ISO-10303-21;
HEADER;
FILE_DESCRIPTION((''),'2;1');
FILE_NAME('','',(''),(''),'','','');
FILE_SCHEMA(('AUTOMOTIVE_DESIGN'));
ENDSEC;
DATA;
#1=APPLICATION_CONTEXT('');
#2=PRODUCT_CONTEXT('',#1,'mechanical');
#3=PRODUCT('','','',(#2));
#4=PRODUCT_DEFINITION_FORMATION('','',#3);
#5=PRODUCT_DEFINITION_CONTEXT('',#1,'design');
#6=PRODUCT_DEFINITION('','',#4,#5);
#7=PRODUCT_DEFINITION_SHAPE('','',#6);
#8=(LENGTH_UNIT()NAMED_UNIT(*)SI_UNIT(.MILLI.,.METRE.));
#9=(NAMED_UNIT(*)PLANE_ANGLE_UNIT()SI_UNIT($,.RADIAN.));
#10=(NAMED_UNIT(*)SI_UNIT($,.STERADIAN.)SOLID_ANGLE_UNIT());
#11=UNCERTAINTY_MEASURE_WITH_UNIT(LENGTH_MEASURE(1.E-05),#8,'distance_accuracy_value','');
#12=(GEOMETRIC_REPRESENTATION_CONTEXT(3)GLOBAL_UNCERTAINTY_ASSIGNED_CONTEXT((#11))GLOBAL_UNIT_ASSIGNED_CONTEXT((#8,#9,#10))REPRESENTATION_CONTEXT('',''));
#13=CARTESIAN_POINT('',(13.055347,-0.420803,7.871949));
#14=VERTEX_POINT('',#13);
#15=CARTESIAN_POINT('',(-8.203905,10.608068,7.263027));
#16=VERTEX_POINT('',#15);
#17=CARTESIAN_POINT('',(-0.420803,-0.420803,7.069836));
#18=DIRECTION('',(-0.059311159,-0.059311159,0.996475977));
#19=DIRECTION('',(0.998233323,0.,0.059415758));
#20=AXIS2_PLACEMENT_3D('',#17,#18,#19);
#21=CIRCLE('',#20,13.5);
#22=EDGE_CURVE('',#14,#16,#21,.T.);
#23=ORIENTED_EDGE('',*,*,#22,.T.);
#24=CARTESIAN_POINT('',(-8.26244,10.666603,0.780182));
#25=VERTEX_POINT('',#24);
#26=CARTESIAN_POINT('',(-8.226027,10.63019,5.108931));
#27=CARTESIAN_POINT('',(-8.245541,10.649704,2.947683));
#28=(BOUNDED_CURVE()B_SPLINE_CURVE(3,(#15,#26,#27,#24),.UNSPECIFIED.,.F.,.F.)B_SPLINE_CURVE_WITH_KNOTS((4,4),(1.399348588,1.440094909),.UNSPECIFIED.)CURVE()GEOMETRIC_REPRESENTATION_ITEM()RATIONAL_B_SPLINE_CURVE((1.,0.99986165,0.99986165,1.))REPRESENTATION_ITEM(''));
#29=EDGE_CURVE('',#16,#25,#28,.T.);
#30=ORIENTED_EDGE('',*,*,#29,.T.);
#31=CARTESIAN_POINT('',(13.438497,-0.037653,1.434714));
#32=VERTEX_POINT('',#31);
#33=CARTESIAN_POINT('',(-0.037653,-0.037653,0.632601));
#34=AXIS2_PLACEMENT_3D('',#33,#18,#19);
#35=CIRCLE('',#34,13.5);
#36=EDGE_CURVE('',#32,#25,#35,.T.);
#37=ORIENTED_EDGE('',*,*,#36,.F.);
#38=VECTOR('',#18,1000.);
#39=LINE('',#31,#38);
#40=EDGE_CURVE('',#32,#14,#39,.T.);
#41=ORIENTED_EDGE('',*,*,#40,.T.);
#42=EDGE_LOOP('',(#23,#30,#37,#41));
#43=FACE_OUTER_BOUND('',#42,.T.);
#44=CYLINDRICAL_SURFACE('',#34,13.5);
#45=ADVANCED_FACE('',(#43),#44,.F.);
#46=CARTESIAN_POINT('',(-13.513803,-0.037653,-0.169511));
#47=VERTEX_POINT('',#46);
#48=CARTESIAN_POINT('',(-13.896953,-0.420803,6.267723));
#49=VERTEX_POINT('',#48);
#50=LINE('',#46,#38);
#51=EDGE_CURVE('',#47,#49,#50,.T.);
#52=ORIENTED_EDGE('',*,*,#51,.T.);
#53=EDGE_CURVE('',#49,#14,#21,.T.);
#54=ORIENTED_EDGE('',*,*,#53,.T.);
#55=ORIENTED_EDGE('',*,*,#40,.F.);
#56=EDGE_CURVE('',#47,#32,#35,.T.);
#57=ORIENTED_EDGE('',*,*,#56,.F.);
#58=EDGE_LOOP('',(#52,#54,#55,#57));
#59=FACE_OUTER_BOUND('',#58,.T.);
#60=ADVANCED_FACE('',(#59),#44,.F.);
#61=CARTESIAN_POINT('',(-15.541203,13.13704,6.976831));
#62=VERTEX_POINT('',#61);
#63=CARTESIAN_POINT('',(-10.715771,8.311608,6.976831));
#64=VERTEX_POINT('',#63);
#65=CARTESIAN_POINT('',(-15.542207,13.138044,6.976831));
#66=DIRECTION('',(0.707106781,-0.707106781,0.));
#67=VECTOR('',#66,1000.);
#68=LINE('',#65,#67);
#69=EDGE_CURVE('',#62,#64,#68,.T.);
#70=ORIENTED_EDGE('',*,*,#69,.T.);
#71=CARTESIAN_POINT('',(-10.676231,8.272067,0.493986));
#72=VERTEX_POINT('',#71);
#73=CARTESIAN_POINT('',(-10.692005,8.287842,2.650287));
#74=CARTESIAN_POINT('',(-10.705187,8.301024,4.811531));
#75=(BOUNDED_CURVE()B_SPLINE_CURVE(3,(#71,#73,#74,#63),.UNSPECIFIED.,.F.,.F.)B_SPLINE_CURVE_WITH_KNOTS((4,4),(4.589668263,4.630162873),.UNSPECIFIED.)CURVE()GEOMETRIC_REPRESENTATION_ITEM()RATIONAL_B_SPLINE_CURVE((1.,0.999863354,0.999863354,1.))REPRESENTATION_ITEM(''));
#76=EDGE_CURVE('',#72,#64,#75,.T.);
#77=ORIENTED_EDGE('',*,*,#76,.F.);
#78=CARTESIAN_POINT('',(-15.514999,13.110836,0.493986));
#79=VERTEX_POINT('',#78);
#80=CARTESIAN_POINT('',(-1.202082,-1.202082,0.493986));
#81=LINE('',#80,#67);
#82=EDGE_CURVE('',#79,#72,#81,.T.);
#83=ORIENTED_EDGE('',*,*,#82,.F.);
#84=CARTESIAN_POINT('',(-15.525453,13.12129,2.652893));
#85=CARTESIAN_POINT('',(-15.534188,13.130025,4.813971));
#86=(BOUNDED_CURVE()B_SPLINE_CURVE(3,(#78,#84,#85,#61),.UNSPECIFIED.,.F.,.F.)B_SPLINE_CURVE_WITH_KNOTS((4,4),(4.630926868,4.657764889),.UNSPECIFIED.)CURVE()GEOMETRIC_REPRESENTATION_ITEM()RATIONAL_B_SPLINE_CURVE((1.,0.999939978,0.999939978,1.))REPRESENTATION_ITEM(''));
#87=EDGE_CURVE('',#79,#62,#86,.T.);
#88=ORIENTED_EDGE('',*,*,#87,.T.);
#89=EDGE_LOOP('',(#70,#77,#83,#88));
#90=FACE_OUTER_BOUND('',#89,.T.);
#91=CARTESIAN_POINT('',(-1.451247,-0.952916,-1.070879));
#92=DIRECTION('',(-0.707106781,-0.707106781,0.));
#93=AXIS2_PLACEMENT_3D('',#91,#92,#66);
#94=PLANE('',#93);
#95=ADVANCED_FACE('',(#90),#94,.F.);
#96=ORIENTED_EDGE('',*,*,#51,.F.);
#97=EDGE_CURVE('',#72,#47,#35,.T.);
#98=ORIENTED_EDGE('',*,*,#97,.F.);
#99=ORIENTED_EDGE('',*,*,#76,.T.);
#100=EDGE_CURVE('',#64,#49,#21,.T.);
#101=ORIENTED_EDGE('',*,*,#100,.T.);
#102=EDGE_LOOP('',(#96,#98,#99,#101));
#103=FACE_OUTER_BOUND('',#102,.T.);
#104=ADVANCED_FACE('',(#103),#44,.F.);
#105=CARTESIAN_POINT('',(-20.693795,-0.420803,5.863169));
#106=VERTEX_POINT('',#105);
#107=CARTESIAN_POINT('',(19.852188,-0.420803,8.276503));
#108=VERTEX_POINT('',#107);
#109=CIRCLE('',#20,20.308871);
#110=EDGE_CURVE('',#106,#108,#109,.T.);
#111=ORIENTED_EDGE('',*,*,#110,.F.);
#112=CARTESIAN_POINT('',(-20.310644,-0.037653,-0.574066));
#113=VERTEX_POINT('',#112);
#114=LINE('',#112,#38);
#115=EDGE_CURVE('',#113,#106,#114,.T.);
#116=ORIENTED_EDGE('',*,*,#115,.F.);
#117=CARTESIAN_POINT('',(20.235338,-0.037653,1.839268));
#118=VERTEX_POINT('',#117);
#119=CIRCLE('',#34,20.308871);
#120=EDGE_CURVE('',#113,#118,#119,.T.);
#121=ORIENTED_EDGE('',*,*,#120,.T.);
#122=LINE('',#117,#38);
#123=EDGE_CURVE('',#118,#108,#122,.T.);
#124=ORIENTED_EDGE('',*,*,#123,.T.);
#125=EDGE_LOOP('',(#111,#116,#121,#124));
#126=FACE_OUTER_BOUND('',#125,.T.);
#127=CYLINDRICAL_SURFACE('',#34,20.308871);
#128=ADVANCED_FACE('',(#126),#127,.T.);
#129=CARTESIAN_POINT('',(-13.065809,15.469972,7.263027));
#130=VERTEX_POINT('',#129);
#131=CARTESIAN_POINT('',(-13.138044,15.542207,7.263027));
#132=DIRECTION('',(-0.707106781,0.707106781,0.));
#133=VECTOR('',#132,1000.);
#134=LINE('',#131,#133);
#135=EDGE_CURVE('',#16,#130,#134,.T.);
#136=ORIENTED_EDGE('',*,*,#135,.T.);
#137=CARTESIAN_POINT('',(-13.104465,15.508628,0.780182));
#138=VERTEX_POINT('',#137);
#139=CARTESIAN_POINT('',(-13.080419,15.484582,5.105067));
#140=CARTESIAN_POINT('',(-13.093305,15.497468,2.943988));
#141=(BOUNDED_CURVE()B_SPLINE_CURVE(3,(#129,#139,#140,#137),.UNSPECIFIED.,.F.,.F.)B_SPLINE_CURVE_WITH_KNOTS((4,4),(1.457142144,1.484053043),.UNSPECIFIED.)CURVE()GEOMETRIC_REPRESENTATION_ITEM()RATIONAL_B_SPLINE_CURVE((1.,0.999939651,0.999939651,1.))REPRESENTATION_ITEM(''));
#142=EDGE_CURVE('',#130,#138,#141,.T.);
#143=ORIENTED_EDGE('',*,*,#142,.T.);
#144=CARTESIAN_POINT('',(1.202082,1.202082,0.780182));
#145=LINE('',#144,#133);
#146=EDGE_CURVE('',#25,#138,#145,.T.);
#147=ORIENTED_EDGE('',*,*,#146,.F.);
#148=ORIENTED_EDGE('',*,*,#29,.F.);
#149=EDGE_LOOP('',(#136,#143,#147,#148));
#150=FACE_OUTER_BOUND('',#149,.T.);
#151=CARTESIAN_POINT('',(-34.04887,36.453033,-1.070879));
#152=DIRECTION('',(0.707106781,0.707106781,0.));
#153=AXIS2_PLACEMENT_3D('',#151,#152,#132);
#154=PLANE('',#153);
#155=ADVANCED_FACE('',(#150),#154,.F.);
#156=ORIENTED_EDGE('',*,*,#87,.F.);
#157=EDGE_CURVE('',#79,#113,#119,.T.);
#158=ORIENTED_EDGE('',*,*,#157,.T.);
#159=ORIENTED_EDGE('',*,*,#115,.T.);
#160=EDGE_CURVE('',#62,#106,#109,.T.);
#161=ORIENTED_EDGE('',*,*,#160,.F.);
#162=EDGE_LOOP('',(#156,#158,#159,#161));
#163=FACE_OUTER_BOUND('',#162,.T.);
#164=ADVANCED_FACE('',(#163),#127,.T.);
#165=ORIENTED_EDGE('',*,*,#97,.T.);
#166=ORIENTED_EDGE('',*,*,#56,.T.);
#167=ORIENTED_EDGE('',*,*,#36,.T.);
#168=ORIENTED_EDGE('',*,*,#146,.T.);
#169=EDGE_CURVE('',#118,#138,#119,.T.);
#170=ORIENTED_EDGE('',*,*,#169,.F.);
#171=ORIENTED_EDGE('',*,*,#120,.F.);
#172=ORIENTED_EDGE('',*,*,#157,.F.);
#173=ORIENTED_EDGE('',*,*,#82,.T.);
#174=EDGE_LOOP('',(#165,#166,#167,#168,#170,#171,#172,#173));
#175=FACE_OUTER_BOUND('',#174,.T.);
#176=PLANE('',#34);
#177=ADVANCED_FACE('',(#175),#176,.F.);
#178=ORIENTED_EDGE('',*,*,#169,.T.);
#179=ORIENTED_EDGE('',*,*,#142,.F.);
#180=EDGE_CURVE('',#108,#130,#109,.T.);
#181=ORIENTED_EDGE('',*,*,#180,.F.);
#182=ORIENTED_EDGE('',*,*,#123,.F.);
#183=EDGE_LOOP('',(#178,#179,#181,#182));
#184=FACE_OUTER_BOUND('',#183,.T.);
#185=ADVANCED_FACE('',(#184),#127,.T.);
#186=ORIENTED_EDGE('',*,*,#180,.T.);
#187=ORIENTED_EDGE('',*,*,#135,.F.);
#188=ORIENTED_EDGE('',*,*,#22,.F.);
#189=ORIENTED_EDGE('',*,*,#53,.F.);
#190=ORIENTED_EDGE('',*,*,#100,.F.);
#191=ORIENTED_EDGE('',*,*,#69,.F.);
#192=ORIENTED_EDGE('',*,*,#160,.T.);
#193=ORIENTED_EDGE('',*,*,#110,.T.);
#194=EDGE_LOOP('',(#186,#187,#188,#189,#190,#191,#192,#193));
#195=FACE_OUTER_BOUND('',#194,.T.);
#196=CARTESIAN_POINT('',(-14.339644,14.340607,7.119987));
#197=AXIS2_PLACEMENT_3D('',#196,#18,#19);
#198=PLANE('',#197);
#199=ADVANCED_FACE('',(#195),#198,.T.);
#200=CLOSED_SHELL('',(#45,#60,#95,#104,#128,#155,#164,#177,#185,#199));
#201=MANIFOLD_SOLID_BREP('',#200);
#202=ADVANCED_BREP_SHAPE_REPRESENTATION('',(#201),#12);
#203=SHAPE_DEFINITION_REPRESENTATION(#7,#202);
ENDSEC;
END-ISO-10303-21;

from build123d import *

# Parameters (mm, degrees)
BASE_EXTRUDE_DEPTH      = 0.001
BASE_EXTRUDE_DEPTH_BACK = 0.001
SKETCH6_W               = 6.42
SKETCH6_H               = 6.76
SKETCH8_R               = 20.30887065
SKETCH8_R_2             = 13.5
BOSS_EXTRUDE1_DEPTH     = 6.46
CUT_EXTRUDE1_DEPTH      = 31.552378082
CUT_EXTRUDE1_DEPTH_BACK = 31.552378082


with BuildPart() as part:
    # Sketch6 → Base-Extrude (new, two sides: drawn at the far end of the back side and taken through both)
    with BuildSketch(Plane(origin=(-9.545941546, 9.545941546, 7.14), x_dir=(0.05931115895295759, 0.059311158952956106, -0.996475977054798), z_dir=(0.7046149206649441, 0.7046149206649323, 0.08387864539133799)).offset(-BASE_EXTRUDE_DEPTH_BACK)):
        with Locations((3.23, 3.4)):
            Rectangle(SKETCH6_W, SKETCH6_H)
    extrude(amount=BASE_EXTRUDE_DEPTH + BASE_EXTRUDE_DEPTH_BACK)

    # Sketch8 → Boss-Extrude1 (add)
    with BuildSketch(Plane(origin=(-0.420803093, -0.420803093, 7.069836103), x_dir=(0.9982394983905275, -0.0038244762114057976, 0.05918848903914046), z_dir=(-0.05931115895295754, -0.05931115895295616, 0.996475977054798))):
        with Locations(Location((0, 0, 0), (0, 0, 0.219513325))):
            Circle(SKETCH8_R)
        with Locations(Location((0, 0, 0), (0, 0, 0.219513325))):
            Circle(SKETCH8_R_2, mode=Mode.SUBTRACT)
    extrude(amount=-BOSS_EXTRUDE1_DEPTH)

    # Sketch9 → Cut-Extrude1 (cut, two sides: drawn at the far end of the back side and taken through both)
    with BuildSketch(Plane.XY.offset(-CUT_EXTRUDE1_DEPTH_BACK)):
        Polygon((-34.048869909, 36.453032965), (0.95291576, 1.451247296), (-1.451247296, -0.95291576), (-38.857196021, 36.453032965), align=None)
    extrude(amount=CUT_EXTRUDE1_DEPTH + CUT_EXTRUDE1_DEPTH_BACK, mode=Mode.SUBTRACT)


solid = part.part
